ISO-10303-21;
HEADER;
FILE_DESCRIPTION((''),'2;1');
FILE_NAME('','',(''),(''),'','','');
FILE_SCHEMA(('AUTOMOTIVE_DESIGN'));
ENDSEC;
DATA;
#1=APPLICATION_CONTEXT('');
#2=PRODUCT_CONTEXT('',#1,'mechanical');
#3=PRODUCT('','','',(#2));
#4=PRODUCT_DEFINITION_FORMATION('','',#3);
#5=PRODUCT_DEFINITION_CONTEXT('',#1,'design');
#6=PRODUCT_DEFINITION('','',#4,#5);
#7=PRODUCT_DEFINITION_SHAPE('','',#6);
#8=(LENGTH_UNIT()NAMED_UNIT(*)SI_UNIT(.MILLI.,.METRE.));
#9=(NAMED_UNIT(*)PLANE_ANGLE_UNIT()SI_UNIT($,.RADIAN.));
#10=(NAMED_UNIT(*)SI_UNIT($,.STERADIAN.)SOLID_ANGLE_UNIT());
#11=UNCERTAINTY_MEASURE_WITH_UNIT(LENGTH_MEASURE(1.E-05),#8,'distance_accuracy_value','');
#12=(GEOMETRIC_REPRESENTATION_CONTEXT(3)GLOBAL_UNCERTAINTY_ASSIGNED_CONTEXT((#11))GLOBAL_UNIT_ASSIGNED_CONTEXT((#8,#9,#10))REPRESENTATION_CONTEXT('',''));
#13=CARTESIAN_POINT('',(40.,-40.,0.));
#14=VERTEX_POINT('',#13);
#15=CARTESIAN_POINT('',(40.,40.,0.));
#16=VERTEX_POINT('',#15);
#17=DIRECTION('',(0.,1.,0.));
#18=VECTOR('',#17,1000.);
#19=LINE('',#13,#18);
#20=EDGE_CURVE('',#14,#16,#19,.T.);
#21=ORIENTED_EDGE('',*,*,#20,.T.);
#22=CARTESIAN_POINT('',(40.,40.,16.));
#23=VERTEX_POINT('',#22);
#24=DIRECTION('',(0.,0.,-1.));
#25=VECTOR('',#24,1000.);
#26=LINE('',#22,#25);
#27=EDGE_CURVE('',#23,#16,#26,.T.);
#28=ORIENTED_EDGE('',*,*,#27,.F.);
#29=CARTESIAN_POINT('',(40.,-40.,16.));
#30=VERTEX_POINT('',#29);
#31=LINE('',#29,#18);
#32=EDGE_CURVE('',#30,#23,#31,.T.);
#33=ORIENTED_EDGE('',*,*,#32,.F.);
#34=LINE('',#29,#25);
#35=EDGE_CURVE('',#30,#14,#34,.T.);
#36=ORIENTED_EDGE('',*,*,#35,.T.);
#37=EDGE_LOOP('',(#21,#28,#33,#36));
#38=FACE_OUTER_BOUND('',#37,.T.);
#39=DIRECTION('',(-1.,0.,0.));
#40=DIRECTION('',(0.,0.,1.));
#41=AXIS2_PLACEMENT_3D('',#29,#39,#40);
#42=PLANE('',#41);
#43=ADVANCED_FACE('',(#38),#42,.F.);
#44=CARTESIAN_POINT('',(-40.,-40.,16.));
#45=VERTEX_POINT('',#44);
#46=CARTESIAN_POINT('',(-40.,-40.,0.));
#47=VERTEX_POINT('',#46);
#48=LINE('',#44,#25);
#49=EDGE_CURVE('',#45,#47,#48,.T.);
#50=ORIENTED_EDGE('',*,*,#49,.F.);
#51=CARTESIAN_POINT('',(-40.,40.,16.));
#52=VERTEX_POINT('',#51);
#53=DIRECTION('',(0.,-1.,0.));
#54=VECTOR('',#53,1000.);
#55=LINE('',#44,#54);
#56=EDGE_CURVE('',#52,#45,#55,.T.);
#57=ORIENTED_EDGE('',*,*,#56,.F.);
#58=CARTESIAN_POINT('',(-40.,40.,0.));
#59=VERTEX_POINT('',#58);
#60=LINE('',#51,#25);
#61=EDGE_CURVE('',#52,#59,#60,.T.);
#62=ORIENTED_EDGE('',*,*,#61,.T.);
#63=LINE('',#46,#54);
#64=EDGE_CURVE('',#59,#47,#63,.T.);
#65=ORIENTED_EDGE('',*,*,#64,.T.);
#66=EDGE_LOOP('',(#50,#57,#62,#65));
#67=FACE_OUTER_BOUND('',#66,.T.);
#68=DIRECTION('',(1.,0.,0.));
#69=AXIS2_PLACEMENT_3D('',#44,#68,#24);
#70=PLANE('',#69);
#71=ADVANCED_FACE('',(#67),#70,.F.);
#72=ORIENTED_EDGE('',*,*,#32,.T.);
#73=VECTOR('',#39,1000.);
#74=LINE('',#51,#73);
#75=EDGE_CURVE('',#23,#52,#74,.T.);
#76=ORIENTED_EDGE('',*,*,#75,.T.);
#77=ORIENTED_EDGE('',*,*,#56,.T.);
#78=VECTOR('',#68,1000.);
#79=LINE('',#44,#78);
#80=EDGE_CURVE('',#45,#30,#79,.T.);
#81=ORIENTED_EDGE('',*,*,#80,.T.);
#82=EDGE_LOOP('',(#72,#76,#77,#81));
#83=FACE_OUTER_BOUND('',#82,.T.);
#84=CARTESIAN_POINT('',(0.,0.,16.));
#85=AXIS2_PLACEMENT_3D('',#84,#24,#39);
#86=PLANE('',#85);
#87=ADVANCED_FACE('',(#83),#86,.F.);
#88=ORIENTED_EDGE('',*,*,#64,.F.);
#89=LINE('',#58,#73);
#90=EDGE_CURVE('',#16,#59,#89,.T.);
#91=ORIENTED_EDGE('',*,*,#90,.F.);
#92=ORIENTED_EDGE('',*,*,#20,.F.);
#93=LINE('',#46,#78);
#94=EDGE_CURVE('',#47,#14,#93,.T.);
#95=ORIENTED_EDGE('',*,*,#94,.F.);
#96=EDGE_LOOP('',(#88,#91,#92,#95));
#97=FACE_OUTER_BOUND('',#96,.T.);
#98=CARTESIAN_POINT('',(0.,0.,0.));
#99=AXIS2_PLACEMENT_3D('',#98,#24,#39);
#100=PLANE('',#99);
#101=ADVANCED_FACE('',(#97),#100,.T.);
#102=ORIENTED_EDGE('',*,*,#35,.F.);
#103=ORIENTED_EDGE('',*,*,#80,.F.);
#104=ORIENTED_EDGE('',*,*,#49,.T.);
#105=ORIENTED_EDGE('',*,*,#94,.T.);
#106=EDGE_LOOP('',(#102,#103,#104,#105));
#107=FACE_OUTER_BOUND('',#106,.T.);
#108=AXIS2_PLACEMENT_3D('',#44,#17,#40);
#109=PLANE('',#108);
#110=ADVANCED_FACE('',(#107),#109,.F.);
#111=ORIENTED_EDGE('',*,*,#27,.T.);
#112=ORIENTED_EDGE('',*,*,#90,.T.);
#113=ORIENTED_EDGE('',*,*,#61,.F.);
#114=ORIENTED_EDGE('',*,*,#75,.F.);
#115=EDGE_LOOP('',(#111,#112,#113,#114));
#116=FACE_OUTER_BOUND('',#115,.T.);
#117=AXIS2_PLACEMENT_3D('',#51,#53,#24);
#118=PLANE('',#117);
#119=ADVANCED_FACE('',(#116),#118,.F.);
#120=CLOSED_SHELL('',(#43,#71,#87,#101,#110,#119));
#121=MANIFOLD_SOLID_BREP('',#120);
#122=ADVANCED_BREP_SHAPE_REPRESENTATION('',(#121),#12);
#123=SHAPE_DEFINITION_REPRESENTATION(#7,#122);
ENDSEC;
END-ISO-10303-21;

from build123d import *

# Parameters (mm, degrees)
SKETCH1_W           = 80
SKETCH1_H           = 80
BOSS_EXTRUDE1_DEPTH = 16


with BuildPart() as part:
    # Sketch1 → Boss-Extrude1 (new body)
    with BuildSketch(Plane.XY):
        Rectangle(SKETCH1_W, SKETCH1_H)
    extrude(amount=BOSS_EXTRUDE1_DEPTH)


solid = part.part
